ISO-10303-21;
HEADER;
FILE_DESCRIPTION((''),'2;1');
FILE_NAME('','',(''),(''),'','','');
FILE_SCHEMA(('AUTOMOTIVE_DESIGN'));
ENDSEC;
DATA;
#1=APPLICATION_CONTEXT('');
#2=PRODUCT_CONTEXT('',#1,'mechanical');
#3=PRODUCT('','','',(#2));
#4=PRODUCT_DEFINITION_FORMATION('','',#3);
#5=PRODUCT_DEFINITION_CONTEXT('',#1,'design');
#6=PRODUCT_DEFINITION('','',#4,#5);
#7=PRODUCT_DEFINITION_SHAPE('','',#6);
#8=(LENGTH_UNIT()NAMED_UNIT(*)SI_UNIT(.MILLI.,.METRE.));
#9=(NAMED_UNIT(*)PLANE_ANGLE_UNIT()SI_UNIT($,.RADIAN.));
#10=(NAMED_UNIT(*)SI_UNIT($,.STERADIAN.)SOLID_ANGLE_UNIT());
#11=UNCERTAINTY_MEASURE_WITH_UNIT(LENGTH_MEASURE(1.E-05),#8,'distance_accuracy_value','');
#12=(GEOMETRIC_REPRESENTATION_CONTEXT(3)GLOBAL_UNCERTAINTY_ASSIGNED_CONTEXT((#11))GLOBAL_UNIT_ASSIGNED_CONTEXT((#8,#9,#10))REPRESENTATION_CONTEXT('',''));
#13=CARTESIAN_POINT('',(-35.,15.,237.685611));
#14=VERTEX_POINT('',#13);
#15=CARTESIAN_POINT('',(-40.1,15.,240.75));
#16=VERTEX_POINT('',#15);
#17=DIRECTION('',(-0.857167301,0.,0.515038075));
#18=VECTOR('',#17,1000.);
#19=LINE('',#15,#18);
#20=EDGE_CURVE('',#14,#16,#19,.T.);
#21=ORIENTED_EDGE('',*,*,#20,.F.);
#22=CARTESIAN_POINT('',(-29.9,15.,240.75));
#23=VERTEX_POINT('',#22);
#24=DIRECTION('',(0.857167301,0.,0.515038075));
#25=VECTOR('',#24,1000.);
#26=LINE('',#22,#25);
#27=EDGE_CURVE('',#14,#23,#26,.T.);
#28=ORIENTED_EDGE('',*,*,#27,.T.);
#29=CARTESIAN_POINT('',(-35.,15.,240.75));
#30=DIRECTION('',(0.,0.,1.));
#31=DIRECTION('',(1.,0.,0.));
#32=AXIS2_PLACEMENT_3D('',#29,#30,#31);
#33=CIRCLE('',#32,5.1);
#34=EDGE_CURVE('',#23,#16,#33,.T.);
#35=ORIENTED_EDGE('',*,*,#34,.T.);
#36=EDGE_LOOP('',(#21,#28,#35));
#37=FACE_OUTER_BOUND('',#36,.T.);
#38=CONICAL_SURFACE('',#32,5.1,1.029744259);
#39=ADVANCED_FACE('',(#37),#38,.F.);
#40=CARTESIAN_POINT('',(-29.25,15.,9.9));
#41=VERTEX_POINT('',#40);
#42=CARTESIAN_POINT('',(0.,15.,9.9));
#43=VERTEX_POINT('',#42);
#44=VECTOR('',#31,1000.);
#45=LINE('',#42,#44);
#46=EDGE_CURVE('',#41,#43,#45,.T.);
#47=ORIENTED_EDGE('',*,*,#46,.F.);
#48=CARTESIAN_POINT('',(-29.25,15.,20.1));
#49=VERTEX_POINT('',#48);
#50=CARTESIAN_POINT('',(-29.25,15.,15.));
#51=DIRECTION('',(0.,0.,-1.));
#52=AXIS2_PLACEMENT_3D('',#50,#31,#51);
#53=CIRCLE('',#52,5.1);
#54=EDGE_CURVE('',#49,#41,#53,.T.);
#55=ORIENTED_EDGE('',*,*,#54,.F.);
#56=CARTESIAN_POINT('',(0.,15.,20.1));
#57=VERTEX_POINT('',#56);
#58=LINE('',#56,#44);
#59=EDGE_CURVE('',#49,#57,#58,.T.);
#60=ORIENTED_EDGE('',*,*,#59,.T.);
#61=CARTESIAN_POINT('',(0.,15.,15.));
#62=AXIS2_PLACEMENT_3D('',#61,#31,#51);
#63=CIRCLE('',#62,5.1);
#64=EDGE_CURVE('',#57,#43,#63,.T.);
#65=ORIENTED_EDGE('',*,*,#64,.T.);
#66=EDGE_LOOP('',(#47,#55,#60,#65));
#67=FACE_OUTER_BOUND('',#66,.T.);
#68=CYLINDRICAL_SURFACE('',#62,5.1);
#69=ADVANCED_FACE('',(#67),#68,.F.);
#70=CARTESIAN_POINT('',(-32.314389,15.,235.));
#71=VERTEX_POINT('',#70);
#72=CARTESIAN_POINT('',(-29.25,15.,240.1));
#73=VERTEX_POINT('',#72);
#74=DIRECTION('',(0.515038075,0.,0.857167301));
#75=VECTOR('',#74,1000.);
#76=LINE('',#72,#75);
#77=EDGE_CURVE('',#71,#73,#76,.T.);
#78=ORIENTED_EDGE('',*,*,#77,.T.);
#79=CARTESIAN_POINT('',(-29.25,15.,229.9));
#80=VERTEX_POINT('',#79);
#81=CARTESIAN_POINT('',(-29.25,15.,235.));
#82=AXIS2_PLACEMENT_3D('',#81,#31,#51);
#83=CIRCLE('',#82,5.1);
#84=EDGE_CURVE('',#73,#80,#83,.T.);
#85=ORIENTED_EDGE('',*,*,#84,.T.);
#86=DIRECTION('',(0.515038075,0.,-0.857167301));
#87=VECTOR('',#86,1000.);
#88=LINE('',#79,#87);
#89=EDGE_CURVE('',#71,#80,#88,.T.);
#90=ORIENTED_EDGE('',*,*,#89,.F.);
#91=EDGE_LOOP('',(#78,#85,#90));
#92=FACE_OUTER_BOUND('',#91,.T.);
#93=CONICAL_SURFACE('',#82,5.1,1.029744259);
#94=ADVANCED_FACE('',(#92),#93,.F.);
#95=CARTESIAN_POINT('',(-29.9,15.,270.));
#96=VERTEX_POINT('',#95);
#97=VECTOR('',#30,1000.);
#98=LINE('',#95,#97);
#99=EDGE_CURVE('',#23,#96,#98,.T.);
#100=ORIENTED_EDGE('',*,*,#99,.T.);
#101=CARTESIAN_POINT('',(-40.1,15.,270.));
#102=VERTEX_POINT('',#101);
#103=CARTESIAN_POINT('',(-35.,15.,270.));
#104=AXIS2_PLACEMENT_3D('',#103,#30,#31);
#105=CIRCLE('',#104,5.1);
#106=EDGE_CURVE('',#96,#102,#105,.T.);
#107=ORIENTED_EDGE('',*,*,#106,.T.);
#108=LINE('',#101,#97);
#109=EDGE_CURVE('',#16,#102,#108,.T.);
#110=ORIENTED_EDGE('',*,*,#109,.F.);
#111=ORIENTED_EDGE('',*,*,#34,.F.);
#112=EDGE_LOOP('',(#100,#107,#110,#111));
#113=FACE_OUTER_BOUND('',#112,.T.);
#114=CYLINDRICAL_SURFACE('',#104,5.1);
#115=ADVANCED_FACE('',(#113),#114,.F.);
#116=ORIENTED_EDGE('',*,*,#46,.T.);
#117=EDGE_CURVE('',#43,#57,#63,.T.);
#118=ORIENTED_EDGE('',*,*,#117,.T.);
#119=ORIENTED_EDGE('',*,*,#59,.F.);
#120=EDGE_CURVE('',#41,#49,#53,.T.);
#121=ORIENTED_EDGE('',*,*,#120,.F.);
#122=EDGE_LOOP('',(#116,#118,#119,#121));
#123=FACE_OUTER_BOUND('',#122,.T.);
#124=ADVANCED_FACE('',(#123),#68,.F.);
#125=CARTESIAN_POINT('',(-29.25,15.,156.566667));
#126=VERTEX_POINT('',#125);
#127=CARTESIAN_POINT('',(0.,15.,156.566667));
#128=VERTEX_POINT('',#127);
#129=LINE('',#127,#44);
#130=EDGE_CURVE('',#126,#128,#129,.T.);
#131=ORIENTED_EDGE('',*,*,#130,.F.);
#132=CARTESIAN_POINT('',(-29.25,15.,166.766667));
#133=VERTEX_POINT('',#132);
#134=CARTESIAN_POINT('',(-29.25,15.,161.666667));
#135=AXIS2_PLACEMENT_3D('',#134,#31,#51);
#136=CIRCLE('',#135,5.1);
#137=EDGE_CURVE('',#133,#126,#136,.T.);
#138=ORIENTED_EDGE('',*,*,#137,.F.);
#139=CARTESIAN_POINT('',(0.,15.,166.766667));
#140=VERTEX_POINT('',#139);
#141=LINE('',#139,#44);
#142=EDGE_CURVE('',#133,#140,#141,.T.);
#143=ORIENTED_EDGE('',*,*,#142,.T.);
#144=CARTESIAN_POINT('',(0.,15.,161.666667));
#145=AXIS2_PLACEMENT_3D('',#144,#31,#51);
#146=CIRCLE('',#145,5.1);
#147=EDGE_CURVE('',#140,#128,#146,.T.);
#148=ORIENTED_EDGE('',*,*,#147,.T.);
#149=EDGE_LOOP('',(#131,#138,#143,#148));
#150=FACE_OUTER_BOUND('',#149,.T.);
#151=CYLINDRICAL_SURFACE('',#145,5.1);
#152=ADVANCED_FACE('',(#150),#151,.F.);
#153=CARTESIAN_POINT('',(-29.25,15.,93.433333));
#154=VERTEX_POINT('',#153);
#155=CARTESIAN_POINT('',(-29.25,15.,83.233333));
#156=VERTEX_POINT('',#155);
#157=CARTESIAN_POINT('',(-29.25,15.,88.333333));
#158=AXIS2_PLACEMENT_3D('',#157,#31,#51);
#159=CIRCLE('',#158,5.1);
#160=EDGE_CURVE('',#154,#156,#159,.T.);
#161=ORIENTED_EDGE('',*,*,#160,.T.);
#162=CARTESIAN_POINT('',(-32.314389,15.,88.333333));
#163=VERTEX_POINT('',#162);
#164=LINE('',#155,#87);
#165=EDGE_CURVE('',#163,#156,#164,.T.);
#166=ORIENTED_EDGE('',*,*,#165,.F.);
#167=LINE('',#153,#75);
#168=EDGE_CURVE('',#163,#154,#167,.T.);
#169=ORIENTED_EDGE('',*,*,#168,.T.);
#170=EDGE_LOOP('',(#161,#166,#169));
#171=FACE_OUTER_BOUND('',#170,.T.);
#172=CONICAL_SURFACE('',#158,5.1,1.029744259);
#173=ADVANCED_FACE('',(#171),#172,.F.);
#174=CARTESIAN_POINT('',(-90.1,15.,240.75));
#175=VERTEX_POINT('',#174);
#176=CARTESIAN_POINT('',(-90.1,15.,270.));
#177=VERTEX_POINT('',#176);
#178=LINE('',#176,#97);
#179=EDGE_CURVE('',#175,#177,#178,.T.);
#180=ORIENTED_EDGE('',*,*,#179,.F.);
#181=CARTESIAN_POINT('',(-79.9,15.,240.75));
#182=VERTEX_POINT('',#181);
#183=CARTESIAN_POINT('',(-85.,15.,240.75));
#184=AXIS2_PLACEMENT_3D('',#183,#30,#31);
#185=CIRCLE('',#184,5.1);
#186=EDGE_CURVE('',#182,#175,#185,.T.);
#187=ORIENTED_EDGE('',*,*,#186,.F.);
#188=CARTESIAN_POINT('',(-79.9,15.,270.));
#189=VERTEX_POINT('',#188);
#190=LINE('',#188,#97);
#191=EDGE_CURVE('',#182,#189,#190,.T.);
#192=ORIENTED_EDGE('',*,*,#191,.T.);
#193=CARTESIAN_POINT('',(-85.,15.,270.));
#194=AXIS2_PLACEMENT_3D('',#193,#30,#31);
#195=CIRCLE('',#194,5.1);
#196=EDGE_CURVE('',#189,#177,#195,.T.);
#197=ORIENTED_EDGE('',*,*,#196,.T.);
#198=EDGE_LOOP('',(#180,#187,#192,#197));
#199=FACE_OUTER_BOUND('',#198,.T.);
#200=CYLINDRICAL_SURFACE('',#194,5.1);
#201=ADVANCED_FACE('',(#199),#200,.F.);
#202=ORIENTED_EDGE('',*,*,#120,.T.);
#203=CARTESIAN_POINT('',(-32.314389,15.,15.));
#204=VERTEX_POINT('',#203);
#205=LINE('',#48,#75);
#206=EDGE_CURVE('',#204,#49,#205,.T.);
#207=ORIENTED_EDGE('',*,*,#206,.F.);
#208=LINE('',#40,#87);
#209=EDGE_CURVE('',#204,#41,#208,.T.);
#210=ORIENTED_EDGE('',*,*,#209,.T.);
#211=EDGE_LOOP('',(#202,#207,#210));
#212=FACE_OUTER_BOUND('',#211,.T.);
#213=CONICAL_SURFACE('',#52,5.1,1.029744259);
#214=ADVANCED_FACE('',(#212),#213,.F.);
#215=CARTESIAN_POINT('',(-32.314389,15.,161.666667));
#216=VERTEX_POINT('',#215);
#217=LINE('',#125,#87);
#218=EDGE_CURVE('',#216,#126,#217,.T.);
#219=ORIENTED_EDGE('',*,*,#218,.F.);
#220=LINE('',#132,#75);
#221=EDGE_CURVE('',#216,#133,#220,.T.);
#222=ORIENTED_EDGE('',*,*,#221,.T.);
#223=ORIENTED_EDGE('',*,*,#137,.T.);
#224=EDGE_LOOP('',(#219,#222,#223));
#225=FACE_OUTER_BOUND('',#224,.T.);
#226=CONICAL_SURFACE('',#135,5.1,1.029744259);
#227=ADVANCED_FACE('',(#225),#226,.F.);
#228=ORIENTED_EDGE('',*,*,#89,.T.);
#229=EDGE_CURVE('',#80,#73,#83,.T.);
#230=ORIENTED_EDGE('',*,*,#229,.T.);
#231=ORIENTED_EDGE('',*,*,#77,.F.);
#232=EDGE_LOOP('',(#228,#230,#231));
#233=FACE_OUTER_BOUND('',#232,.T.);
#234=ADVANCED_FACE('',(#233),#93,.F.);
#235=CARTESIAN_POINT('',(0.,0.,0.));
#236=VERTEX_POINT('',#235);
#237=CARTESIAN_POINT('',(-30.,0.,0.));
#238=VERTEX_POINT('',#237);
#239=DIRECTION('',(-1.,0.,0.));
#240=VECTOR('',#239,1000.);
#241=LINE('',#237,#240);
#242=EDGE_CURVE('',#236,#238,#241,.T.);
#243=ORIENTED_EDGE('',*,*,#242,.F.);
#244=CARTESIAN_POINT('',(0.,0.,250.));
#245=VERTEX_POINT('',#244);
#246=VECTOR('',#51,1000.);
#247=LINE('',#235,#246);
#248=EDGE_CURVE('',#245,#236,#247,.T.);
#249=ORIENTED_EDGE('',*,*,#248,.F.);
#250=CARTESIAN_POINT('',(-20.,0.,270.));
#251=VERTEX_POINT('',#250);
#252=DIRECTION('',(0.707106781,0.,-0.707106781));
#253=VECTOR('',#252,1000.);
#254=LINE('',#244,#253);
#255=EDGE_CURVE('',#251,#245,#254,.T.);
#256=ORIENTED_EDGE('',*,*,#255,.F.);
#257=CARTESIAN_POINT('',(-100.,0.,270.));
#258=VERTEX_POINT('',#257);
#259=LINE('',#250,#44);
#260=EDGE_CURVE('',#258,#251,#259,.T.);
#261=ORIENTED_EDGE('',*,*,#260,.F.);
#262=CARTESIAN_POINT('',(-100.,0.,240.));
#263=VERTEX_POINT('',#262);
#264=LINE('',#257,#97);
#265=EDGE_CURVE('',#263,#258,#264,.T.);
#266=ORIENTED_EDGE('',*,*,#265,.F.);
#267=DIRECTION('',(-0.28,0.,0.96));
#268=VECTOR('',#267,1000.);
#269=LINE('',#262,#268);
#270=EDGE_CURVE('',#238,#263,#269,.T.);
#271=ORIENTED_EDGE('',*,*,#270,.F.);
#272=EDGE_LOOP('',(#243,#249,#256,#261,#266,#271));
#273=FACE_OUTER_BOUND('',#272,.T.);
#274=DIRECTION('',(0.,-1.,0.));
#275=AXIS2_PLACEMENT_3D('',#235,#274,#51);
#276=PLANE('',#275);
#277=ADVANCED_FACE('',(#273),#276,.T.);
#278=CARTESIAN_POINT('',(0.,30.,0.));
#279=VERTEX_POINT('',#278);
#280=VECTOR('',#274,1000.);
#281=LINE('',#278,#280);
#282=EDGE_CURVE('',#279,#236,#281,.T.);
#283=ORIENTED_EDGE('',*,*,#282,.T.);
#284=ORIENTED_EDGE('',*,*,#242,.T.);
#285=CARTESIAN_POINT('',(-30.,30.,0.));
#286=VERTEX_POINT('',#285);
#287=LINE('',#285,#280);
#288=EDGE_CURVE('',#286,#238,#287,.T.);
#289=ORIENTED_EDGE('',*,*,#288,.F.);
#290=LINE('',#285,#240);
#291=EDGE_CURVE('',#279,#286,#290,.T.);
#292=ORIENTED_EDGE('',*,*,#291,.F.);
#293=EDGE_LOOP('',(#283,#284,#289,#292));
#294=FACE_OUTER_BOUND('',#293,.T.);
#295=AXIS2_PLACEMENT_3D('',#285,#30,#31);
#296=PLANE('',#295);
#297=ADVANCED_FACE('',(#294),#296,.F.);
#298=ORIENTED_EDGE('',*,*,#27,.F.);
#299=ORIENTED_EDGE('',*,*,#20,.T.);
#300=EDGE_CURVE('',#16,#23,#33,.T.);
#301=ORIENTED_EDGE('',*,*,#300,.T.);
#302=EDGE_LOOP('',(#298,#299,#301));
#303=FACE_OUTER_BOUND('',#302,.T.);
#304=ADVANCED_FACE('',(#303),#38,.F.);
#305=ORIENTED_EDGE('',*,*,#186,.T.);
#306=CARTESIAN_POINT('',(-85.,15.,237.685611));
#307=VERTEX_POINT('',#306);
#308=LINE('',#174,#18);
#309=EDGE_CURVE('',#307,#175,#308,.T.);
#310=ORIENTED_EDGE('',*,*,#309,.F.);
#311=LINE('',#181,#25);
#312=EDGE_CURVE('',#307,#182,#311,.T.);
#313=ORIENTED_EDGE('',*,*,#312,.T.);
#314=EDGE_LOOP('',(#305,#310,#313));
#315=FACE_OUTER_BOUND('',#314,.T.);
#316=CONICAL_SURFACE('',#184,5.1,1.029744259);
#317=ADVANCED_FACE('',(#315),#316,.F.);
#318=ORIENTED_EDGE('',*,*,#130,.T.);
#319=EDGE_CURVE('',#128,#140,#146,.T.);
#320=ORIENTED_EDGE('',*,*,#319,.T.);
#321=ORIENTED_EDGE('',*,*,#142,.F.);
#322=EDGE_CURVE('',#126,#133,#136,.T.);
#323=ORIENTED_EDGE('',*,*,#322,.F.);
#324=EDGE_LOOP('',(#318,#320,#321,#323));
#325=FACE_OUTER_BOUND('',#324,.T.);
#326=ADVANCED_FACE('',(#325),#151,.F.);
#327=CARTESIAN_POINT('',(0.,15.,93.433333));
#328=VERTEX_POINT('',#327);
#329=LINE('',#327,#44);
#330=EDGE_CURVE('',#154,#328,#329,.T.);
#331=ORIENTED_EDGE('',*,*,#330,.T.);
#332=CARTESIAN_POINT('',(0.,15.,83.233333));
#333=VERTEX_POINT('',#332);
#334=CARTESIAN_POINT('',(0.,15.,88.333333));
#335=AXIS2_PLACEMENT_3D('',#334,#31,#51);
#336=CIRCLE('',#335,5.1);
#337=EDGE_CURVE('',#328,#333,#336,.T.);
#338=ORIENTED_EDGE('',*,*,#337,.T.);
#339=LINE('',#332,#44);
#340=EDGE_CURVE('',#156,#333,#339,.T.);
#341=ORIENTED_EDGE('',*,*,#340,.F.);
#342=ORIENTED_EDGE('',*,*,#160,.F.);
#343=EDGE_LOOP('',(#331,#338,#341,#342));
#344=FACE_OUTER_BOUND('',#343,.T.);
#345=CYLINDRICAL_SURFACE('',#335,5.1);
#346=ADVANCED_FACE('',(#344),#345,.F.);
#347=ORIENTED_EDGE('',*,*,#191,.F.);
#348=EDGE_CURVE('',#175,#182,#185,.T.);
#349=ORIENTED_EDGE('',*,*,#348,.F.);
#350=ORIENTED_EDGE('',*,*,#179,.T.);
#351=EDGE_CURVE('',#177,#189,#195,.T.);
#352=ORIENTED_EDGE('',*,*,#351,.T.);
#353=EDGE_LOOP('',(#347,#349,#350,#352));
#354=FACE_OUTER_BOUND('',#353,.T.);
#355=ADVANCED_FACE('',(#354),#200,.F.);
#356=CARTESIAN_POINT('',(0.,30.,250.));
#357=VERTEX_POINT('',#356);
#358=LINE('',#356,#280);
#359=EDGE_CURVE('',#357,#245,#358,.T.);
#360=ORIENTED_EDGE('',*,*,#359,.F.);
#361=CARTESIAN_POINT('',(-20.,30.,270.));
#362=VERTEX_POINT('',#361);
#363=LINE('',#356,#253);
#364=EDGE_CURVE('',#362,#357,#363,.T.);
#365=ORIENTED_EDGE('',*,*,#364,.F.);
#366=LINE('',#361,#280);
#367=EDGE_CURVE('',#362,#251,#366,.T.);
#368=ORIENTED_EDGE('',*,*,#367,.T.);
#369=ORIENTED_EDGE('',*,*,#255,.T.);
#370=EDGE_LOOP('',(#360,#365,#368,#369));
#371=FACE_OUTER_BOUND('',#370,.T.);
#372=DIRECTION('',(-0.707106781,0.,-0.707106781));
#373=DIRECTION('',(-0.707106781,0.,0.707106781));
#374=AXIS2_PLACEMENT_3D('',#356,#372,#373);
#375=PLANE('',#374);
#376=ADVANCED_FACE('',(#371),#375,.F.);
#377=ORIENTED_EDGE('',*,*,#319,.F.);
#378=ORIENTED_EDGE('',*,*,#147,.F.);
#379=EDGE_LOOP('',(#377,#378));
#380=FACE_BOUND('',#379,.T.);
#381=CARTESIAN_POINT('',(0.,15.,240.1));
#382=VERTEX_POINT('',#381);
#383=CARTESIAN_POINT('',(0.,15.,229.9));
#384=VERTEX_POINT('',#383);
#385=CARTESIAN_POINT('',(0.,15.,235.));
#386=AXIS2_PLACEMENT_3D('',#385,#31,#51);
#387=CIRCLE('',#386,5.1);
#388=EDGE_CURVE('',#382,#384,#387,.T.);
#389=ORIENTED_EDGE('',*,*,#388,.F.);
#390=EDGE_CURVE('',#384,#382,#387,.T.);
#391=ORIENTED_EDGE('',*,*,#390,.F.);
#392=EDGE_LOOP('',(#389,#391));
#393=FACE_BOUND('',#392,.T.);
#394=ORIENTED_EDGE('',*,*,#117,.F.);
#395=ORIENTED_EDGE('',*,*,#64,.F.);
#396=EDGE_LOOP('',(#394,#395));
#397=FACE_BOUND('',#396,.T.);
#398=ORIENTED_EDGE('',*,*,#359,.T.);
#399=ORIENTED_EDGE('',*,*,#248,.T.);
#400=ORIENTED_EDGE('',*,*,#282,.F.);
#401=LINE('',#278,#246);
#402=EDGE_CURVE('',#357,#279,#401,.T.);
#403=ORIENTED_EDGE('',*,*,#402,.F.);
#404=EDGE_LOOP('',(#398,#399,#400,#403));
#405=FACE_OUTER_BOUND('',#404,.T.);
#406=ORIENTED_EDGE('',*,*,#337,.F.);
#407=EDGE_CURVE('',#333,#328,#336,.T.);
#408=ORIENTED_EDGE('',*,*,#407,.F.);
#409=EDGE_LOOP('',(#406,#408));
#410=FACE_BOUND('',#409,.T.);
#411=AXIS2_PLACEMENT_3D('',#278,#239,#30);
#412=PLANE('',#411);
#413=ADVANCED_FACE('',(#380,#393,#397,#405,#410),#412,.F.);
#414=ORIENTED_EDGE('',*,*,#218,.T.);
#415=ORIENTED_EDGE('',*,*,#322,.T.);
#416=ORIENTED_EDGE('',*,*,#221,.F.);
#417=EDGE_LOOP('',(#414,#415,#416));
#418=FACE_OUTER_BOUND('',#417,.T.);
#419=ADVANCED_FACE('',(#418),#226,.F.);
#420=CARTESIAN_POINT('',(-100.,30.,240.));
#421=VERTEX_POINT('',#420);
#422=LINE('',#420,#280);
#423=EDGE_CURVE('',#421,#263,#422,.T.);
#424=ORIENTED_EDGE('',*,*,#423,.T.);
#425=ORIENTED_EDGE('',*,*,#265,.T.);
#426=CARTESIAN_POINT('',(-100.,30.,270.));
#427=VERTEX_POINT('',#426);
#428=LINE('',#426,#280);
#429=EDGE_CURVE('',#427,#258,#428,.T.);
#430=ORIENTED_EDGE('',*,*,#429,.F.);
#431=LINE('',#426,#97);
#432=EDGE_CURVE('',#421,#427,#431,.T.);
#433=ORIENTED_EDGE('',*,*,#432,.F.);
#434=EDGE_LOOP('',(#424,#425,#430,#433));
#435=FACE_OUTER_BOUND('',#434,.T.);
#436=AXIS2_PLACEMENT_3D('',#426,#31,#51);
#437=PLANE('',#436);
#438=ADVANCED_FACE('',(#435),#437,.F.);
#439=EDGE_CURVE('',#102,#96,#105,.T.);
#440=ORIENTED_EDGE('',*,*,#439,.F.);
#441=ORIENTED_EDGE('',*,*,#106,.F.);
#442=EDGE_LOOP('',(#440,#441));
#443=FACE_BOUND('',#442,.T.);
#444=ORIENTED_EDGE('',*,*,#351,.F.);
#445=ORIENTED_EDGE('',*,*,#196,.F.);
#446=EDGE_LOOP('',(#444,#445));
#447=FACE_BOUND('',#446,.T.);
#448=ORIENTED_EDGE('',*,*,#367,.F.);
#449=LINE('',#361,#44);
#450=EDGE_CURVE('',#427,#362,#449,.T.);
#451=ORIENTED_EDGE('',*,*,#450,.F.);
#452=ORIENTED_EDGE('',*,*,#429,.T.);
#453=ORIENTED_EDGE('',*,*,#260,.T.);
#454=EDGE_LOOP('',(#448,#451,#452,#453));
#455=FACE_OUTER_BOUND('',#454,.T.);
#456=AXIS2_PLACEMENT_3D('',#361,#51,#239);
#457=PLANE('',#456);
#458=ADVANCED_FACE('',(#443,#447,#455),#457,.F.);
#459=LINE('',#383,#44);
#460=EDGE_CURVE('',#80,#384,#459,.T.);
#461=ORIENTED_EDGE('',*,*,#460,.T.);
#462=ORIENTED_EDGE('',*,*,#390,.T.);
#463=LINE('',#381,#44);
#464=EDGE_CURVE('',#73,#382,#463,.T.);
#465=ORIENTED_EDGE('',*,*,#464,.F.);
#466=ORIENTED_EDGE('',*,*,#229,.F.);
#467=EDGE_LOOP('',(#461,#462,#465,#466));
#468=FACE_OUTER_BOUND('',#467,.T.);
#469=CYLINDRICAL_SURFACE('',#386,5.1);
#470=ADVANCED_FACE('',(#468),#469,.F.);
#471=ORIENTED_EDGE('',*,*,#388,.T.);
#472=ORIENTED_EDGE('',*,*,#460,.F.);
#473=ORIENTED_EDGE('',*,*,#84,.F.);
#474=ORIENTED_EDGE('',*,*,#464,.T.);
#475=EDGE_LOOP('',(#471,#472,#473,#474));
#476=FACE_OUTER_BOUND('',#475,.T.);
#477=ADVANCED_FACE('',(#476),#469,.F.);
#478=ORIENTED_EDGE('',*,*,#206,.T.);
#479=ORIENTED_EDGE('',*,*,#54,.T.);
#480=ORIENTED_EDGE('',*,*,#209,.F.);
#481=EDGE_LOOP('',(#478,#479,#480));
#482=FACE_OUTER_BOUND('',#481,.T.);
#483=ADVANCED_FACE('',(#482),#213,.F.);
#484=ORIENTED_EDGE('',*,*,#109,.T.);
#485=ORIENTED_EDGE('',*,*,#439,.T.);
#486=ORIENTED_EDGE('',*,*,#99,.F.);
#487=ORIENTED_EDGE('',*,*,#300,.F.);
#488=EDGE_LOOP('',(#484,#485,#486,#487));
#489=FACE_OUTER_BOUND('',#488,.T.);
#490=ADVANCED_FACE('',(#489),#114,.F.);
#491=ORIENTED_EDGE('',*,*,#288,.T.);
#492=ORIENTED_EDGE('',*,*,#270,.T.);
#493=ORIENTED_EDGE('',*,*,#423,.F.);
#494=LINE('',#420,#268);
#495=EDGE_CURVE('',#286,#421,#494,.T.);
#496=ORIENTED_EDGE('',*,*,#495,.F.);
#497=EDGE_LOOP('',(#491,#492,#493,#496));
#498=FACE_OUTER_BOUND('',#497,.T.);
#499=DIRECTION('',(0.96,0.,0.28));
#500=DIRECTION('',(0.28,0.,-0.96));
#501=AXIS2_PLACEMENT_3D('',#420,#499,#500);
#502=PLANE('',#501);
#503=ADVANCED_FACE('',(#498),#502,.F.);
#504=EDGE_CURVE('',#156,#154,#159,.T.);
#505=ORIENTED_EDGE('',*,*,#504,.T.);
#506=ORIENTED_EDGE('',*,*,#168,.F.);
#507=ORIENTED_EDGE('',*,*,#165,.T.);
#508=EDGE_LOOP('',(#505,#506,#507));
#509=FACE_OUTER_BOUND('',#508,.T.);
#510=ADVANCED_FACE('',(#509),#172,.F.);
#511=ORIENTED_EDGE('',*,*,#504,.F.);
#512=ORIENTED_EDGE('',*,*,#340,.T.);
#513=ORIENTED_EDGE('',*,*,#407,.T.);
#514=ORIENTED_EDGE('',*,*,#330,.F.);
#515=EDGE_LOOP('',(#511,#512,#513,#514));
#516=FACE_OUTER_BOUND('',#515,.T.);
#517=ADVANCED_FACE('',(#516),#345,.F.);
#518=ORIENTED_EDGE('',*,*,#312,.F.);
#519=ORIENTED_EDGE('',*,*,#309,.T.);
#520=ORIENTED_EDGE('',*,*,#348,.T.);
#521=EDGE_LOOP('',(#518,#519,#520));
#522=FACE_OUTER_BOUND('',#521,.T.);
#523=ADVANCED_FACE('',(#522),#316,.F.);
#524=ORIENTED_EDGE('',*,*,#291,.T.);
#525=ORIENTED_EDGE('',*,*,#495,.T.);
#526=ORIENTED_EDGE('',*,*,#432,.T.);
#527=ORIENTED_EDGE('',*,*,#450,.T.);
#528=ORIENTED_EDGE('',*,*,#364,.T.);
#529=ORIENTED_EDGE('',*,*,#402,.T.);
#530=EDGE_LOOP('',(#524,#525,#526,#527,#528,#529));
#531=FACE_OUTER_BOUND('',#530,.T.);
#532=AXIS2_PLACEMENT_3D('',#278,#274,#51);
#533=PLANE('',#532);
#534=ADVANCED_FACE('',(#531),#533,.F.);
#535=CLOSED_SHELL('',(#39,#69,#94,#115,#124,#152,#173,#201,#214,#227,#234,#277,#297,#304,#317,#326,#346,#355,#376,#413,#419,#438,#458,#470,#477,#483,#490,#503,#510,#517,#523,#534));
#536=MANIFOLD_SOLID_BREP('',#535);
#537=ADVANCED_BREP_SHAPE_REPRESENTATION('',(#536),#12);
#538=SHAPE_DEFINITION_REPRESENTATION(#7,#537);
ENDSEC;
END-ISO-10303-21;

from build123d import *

# Parameters (mm, degrees)
EXTRUDE_1_DEPTH         = 30
HOLE_WIZARD_M12_1_D     = 10.2
HOLE_WIZARD_M12_1_DEPTH = 29.25
HOLE_WIZARD_M12_1_TIP   = 3.064389157
HOLE_WIZARD_M12_2_D     = 10.2
HOLE_WIZARD_M12_2_DEPTH = 29.25
HOLE_WIZARD_M12_2_TIP   = 3.064389157


with BuildPart() as part:
    # 草图1 → 凸台-拉伸1 (new body)
    with BuildSketch(Plane(origin=(0, 0, 0), x_dir=(1, 0, 0), z_dir=(0, 1, 0))):
        Polygon((0, 0), (0, -250), (-20, -270), (-100, -270), (-100, -240), (-30, 0), align=None)
    extrude(amount=EXTRUDE_1_DEPTH)

    # M12 螺纹孔1
    with Locations(Plane(origin=(0, 0, 0), x_dir=(0, 0, -1), z_dir=(1, 0, 0))):
        with Locations((-235, 15), (-15, 15), (-88.333333333, 15), (-161.666666667, 15)):
            Hole(HOLE_WIZARD_M12_1_D / 2, depth=HOLE_WIZARD_M12_1_DEPTH)
            with Locations((0, 0, -(HOLE_WIZARD_M12_1_DEPTH + HOLE_WIZARD_M12_1_TIP / 2))):  # 118° drill point
                Cone(0, HOLE_WIZARD_M12_1_D / 2, HOLE_WIZARD_M12_1_TIP, mode=Mode.SUBTRACT)

    # M12 螺纹孔2
    with Locations(Plane.XY.offset(270)):
        with Locations((-35, 15), (-85, 15)):
            Hole(HOLE_WIZARD_M12_2_D / 2, depth=HOLE_WIZARD_M12_2_DEPTH)
            with Locations((0, 0, -(HOLE_WIZARD_M12_2_DEPTH + HOLE_WIZARD_M12_2_TIP / 2))):  # 118° drill point
                Cone(0, HOLE_WIZARD_M12_2_D / 2, HOLE_WIZARD_M12_2_TIP, mode=Mode.SUBTRACT)


solid = part.part
